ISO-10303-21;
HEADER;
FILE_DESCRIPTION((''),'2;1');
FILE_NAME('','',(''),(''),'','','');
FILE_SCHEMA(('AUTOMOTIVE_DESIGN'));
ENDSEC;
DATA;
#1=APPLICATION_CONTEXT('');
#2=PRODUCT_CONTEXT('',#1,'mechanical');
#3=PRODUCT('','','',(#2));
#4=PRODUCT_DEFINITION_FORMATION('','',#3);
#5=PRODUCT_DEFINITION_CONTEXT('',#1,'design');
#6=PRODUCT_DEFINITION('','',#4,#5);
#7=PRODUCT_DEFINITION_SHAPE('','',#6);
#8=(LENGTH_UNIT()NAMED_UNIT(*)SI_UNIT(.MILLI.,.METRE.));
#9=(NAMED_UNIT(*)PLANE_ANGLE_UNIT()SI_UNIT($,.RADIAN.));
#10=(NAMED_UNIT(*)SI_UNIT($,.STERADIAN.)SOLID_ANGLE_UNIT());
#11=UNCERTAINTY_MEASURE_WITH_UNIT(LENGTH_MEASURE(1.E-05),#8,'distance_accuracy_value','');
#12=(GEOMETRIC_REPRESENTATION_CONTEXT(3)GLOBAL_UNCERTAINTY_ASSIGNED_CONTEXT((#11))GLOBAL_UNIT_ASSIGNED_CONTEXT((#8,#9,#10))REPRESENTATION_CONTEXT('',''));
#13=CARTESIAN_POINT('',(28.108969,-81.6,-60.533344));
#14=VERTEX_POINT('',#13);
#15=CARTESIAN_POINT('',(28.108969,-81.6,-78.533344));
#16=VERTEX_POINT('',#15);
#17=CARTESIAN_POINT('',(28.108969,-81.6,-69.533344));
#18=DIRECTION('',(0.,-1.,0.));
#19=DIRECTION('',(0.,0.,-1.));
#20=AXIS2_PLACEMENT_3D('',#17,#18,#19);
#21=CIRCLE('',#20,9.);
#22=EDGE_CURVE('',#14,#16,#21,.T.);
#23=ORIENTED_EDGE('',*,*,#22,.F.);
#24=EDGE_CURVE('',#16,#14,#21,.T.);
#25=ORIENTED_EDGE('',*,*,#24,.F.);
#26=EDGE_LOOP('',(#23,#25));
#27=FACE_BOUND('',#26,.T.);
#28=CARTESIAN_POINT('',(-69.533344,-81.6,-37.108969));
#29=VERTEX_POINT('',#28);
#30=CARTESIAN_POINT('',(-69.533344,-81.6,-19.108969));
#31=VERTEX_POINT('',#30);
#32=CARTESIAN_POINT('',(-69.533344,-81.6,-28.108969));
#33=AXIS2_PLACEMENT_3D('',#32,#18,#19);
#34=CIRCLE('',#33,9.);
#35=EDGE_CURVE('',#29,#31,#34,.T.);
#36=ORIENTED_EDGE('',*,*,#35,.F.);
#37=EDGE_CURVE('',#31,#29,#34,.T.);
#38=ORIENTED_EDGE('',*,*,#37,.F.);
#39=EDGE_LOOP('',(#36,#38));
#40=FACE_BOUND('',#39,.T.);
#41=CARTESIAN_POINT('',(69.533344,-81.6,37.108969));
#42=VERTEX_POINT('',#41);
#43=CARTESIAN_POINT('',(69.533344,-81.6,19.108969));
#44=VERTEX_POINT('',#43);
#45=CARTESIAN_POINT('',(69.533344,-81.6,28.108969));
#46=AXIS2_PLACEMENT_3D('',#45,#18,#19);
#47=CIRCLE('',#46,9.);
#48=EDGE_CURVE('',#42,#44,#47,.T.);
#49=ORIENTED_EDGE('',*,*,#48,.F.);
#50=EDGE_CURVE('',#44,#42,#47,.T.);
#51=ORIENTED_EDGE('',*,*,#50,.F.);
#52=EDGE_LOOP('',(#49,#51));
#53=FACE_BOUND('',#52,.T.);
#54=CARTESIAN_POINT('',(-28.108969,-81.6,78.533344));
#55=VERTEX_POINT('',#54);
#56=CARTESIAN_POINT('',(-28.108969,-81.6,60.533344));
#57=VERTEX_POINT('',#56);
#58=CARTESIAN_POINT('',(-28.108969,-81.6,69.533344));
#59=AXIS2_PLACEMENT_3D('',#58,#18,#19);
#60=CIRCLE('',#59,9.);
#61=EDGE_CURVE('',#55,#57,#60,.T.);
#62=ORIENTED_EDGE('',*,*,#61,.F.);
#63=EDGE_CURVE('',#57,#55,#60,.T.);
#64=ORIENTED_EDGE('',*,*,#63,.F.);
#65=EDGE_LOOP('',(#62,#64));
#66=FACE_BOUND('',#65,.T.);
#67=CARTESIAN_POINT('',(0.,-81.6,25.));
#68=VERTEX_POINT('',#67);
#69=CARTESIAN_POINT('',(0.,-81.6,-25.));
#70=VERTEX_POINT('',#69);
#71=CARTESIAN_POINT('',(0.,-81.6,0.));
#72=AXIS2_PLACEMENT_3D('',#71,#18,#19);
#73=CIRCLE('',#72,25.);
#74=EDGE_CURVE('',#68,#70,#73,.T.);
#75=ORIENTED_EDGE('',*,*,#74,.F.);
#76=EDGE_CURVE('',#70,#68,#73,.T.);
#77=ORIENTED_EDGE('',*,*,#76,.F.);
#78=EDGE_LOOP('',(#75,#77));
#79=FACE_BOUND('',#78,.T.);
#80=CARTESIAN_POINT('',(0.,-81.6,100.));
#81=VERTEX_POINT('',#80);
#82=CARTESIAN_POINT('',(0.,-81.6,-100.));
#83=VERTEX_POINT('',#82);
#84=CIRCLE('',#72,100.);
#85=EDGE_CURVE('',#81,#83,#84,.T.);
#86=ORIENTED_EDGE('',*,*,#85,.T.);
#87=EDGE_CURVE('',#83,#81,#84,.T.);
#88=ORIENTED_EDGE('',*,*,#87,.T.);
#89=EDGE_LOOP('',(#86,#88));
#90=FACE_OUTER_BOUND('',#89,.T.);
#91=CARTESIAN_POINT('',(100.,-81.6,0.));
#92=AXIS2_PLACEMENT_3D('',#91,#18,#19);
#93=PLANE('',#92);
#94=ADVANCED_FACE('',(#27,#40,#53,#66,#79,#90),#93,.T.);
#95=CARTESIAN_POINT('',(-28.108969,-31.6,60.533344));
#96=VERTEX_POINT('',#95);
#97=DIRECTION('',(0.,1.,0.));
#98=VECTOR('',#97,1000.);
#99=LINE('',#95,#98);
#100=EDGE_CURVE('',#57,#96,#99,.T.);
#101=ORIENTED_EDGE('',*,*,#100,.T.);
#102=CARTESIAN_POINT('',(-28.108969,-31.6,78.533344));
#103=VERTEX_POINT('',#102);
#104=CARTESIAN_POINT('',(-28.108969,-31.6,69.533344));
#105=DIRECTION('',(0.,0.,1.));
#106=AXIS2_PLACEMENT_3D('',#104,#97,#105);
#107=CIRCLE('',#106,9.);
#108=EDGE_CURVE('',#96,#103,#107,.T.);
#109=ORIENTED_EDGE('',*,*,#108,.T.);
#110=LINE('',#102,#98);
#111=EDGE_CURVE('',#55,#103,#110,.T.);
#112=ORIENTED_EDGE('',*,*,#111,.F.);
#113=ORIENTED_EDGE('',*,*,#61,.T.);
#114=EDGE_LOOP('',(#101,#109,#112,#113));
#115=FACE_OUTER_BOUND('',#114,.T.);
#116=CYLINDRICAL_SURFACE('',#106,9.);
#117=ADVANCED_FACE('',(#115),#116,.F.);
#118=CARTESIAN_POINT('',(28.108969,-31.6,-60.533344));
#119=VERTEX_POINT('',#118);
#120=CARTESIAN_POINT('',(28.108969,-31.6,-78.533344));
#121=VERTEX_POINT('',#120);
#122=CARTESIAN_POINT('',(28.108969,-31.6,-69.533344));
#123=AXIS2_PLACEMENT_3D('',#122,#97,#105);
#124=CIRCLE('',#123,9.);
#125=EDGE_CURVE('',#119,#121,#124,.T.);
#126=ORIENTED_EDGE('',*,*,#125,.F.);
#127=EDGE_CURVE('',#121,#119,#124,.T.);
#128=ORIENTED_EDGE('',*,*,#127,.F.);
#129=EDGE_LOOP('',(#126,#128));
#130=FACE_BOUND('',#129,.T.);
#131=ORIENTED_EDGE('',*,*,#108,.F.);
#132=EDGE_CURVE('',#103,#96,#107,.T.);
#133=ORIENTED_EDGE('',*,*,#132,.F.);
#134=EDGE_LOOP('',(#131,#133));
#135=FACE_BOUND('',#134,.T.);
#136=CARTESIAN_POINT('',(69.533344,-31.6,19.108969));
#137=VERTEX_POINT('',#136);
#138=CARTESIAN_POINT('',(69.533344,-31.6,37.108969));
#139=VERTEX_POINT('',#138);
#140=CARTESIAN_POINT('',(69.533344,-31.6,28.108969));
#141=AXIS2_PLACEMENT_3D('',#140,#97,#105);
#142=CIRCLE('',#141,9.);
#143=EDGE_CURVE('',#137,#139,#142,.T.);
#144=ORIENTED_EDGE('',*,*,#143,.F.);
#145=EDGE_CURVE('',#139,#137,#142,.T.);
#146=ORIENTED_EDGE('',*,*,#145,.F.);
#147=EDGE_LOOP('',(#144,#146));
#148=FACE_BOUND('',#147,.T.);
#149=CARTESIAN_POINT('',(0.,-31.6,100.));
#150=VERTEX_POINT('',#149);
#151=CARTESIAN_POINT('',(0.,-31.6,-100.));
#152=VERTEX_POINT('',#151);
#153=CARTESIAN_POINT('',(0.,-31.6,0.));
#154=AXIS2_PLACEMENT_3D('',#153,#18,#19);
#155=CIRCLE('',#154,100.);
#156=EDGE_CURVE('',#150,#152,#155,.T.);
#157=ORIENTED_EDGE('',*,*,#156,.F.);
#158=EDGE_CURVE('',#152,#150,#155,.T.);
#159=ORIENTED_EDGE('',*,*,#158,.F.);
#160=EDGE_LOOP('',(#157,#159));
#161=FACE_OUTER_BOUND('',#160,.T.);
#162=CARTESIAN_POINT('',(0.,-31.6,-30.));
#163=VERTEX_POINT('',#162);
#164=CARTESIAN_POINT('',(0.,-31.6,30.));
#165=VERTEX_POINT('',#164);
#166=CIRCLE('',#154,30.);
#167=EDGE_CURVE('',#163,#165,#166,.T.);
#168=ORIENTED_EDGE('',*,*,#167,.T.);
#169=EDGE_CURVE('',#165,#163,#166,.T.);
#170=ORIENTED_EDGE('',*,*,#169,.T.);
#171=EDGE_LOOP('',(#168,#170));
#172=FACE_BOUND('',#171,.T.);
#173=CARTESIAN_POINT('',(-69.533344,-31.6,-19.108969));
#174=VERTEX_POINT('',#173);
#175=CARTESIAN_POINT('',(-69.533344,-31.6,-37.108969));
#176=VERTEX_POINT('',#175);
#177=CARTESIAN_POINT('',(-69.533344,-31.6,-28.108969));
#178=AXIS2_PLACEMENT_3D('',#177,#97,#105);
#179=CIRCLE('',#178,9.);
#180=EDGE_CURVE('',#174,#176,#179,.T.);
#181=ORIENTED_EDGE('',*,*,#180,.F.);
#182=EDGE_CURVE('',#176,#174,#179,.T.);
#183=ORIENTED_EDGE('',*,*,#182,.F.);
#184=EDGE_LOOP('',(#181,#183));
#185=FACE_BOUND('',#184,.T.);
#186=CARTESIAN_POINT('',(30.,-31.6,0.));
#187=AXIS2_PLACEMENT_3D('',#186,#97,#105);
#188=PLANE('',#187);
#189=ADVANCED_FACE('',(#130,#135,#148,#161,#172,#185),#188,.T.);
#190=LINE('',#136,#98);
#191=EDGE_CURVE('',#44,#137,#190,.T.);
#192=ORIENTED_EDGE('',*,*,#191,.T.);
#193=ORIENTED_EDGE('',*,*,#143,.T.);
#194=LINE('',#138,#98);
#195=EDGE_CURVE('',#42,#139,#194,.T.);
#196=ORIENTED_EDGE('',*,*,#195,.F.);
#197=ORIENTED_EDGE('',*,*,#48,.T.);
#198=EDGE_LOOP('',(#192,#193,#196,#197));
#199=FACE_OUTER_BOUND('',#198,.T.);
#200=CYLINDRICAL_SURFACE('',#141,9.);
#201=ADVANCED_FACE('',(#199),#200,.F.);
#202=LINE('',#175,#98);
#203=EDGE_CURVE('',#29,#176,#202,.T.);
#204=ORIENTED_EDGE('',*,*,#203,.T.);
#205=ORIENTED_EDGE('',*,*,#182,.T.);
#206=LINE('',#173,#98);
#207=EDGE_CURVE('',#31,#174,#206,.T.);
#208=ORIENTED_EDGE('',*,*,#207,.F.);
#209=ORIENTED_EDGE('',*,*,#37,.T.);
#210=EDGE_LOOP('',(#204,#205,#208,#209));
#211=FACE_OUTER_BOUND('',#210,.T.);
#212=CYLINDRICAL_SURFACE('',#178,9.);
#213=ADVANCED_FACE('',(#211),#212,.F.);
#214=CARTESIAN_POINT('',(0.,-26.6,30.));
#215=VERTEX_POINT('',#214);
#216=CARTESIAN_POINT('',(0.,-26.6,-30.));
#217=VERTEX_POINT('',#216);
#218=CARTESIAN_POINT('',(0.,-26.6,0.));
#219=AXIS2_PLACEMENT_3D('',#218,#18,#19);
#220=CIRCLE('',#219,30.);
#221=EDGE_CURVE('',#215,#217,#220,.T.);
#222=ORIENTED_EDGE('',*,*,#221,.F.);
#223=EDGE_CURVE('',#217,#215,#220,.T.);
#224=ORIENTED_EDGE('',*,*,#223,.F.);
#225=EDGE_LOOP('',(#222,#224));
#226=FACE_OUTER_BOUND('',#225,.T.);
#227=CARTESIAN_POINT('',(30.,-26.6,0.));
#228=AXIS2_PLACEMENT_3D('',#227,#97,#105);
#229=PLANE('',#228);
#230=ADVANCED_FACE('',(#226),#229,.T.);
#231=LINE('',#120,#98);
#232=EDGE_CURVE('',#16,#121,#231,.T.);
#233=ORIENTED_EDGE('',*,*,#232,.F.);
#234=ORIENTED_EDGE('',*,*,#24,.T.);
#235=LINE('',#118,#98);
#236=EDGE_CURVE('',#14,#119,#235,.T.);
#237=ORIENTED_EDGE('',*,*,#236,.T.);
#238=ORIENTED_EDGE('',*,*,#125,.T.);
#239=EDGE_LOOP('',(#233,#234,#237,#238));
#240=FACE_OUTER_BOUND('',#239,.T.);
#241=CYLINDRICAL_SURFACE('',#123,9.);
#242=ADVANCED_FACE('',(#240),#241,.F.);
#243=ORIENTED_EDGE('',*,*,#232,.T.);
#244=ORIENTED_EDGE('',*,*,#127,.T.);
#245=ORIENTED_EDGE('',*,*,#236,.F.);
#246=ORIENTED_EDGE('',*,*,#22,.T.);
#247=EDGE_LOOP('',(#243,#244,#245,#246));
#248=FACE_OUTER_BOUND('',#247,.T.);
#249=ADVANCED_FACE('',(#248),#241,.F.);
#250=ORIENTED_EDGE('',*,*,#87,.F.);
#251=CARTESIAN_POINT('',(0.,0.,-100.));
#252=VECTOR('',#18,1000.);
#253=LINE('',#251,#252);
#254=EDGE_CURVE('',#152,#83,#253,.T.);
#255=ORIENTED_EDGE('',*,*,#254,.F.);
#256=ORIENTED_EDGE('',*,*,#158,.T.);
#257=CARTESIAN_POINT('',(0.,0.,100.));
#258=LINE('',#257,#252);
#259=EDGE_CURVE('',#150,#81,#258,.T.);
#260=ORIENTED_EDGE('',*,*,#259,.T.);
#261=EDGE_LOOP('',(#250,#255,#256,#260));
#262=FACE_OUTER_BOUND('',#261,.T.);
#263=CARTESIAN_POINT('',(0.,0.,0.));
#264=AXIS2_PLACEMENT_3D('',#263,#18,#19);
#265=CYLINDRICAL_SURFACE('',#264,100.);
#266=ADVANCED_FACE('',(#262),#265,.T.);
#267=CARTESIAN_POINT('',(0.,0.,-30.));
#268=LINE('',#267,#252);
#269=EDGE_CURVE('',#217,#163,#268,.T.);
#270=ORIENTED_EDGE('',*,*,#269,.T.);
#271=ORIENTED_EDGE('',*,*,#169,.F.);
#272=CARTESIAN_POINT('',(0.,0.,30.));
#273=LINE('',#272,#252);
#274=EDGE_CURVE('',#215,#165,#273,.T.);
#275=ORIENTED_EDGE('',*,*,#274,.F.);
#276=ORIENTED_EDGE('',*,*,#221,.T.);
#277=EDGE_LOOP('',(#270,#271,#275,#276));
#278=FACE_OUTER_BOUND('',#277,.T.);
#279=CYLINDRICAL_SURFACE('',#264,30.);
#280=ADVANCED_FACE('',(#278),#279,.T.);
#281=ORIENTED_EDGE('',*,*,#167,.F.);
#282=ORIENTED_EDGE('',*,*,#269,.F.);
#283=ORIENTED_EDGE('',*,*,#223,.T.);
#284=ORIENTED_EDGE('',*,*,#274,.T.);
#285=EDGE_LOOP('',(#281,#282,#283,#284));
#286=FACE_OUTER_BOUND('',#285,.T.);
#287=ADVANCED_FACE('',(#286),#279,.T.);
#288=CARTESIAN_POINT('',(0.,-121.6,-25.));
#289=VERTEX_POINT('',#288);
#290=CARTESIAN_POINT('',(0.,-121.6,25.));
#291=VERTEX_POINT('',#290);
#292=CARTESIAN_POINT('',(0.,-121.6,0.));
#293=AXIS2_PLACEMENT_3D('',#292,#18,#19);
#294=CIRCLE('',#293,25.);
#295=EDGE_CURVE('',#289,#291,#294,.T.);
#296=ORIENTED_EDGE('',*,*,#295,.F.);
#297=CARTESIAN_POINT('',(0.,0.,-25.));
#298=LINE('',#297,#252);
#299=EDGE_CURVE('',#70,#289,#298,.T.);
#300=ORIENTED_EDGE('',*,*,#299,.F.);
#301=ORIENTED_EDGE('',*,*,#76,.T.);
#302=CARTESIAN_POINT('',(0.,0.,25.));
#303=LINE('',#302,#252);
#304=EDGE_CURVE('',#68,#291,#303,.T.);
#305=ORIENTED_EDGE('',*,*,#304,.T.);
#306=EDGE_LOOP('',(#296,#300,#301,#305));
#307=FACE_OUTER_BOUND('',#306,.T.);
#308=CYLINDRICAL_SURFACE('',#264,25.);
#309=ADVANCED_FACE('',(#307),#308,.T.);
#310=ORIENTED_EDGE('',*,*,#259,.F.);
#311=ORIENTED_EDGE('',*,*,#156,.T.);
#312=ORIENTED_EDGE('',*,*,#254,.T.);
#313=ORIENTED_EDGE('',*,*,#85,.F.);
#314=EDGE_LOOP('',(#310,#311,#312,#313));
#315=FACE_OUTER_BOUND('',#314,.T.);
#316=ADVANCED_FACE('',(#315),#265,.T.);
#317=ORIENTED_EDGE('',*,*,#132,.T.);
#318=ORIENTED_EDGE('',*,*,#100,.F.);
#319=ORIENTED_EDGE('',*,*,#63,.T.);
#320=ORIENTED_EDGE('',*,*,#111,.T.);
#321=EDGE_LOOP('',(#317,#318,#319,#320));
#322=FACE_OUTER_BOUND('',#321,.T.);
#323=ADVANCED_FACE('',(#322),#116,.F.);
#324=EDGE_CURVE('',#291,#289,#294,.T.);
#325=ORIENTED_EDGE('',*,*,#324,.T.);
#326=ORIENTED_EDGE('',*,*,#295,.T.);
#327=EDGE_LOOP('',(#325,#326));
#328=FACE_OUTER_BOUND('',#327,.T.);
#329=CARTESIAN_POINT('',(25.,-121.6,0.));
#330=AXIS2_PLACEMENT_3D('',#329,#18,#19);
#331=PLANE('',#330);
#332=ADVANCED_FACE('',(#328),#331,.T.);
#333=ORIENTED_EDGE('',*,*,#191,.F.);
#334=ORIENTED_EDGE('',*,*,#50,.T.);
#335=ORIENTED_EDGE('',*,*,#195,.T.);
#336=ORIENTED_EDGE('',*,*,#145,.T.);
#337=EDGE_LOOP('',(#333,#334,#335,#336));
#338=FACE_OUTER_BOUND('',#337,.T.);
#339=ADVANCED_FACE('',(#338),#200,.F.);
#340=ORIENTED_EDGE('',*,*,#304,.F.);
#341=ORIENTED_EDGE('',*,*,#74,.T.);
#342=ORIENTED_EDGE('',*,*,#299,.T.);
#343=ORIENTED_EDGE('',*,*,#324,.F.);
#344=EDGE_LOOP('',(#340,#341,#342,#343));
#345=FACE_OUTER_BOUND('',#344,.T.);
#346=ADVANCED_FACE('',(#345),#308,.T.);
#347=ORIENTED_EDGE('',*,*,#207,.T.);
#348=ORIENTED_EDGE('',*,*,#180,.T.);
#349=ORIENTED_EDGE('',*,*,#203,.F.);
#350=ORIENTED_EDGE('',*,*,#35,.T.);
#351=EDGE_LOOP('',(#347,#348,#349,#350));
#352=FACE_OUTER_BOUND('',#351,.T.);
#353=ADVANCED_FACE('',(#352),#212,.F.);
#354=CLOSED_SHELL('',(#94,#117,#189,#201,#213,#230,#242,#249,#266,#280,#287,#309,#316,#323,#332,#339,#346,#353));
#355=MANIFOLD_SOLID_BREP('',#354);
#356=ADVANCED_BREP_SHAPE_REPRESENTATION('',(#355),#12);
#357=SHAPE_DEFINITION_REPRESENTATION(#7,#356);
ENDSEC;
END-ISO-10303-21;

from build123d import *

# Parameters (mm, degrees)
F_18_0_18_DIAMETER_HOLE1_D     = 18
F_18_0_18_DIAMETER_HOLE1_DEPTH = 90


with BuildPart() as part:
    # Sketch1 → Revolve1 (revolve)
    with BuildSketch(Plane.XY, mode=Mode.PRIVATE) as revolve1_sk:
        Polygon((30, -31.6), (100, -31.6), (100, -81.6), (25, -81.6), (25, -121.6), (0, -121.6), (0, -26.6), (30, -26.6), align=None)
    revolve(revolve1_sk.sketch.rotate(Axis((0, 0, 0), (0, 1, 0)), 90), axis=Axis((0, 0, 0), (0, 1, 0)))

    # Ø18.0 (18) Diameter Hole1
    with Locations(Plane(origin=(0, -31.6, 0), x_dir=(1, 0, 0), z_dir=(0, 1, 0))):
        with Locations((-69.533343678, 28.108968621), (-28.108968621, -69.533343678), (69.533343678, -28.108968621), (28.108968621, 69.533343678)):
            Hole(F_18_0_18_DIAMETER_HOLE1_D / 2, depth=F_18_0_18_DIAMETER_HOLE1_DEPTH)


solid = part.part
